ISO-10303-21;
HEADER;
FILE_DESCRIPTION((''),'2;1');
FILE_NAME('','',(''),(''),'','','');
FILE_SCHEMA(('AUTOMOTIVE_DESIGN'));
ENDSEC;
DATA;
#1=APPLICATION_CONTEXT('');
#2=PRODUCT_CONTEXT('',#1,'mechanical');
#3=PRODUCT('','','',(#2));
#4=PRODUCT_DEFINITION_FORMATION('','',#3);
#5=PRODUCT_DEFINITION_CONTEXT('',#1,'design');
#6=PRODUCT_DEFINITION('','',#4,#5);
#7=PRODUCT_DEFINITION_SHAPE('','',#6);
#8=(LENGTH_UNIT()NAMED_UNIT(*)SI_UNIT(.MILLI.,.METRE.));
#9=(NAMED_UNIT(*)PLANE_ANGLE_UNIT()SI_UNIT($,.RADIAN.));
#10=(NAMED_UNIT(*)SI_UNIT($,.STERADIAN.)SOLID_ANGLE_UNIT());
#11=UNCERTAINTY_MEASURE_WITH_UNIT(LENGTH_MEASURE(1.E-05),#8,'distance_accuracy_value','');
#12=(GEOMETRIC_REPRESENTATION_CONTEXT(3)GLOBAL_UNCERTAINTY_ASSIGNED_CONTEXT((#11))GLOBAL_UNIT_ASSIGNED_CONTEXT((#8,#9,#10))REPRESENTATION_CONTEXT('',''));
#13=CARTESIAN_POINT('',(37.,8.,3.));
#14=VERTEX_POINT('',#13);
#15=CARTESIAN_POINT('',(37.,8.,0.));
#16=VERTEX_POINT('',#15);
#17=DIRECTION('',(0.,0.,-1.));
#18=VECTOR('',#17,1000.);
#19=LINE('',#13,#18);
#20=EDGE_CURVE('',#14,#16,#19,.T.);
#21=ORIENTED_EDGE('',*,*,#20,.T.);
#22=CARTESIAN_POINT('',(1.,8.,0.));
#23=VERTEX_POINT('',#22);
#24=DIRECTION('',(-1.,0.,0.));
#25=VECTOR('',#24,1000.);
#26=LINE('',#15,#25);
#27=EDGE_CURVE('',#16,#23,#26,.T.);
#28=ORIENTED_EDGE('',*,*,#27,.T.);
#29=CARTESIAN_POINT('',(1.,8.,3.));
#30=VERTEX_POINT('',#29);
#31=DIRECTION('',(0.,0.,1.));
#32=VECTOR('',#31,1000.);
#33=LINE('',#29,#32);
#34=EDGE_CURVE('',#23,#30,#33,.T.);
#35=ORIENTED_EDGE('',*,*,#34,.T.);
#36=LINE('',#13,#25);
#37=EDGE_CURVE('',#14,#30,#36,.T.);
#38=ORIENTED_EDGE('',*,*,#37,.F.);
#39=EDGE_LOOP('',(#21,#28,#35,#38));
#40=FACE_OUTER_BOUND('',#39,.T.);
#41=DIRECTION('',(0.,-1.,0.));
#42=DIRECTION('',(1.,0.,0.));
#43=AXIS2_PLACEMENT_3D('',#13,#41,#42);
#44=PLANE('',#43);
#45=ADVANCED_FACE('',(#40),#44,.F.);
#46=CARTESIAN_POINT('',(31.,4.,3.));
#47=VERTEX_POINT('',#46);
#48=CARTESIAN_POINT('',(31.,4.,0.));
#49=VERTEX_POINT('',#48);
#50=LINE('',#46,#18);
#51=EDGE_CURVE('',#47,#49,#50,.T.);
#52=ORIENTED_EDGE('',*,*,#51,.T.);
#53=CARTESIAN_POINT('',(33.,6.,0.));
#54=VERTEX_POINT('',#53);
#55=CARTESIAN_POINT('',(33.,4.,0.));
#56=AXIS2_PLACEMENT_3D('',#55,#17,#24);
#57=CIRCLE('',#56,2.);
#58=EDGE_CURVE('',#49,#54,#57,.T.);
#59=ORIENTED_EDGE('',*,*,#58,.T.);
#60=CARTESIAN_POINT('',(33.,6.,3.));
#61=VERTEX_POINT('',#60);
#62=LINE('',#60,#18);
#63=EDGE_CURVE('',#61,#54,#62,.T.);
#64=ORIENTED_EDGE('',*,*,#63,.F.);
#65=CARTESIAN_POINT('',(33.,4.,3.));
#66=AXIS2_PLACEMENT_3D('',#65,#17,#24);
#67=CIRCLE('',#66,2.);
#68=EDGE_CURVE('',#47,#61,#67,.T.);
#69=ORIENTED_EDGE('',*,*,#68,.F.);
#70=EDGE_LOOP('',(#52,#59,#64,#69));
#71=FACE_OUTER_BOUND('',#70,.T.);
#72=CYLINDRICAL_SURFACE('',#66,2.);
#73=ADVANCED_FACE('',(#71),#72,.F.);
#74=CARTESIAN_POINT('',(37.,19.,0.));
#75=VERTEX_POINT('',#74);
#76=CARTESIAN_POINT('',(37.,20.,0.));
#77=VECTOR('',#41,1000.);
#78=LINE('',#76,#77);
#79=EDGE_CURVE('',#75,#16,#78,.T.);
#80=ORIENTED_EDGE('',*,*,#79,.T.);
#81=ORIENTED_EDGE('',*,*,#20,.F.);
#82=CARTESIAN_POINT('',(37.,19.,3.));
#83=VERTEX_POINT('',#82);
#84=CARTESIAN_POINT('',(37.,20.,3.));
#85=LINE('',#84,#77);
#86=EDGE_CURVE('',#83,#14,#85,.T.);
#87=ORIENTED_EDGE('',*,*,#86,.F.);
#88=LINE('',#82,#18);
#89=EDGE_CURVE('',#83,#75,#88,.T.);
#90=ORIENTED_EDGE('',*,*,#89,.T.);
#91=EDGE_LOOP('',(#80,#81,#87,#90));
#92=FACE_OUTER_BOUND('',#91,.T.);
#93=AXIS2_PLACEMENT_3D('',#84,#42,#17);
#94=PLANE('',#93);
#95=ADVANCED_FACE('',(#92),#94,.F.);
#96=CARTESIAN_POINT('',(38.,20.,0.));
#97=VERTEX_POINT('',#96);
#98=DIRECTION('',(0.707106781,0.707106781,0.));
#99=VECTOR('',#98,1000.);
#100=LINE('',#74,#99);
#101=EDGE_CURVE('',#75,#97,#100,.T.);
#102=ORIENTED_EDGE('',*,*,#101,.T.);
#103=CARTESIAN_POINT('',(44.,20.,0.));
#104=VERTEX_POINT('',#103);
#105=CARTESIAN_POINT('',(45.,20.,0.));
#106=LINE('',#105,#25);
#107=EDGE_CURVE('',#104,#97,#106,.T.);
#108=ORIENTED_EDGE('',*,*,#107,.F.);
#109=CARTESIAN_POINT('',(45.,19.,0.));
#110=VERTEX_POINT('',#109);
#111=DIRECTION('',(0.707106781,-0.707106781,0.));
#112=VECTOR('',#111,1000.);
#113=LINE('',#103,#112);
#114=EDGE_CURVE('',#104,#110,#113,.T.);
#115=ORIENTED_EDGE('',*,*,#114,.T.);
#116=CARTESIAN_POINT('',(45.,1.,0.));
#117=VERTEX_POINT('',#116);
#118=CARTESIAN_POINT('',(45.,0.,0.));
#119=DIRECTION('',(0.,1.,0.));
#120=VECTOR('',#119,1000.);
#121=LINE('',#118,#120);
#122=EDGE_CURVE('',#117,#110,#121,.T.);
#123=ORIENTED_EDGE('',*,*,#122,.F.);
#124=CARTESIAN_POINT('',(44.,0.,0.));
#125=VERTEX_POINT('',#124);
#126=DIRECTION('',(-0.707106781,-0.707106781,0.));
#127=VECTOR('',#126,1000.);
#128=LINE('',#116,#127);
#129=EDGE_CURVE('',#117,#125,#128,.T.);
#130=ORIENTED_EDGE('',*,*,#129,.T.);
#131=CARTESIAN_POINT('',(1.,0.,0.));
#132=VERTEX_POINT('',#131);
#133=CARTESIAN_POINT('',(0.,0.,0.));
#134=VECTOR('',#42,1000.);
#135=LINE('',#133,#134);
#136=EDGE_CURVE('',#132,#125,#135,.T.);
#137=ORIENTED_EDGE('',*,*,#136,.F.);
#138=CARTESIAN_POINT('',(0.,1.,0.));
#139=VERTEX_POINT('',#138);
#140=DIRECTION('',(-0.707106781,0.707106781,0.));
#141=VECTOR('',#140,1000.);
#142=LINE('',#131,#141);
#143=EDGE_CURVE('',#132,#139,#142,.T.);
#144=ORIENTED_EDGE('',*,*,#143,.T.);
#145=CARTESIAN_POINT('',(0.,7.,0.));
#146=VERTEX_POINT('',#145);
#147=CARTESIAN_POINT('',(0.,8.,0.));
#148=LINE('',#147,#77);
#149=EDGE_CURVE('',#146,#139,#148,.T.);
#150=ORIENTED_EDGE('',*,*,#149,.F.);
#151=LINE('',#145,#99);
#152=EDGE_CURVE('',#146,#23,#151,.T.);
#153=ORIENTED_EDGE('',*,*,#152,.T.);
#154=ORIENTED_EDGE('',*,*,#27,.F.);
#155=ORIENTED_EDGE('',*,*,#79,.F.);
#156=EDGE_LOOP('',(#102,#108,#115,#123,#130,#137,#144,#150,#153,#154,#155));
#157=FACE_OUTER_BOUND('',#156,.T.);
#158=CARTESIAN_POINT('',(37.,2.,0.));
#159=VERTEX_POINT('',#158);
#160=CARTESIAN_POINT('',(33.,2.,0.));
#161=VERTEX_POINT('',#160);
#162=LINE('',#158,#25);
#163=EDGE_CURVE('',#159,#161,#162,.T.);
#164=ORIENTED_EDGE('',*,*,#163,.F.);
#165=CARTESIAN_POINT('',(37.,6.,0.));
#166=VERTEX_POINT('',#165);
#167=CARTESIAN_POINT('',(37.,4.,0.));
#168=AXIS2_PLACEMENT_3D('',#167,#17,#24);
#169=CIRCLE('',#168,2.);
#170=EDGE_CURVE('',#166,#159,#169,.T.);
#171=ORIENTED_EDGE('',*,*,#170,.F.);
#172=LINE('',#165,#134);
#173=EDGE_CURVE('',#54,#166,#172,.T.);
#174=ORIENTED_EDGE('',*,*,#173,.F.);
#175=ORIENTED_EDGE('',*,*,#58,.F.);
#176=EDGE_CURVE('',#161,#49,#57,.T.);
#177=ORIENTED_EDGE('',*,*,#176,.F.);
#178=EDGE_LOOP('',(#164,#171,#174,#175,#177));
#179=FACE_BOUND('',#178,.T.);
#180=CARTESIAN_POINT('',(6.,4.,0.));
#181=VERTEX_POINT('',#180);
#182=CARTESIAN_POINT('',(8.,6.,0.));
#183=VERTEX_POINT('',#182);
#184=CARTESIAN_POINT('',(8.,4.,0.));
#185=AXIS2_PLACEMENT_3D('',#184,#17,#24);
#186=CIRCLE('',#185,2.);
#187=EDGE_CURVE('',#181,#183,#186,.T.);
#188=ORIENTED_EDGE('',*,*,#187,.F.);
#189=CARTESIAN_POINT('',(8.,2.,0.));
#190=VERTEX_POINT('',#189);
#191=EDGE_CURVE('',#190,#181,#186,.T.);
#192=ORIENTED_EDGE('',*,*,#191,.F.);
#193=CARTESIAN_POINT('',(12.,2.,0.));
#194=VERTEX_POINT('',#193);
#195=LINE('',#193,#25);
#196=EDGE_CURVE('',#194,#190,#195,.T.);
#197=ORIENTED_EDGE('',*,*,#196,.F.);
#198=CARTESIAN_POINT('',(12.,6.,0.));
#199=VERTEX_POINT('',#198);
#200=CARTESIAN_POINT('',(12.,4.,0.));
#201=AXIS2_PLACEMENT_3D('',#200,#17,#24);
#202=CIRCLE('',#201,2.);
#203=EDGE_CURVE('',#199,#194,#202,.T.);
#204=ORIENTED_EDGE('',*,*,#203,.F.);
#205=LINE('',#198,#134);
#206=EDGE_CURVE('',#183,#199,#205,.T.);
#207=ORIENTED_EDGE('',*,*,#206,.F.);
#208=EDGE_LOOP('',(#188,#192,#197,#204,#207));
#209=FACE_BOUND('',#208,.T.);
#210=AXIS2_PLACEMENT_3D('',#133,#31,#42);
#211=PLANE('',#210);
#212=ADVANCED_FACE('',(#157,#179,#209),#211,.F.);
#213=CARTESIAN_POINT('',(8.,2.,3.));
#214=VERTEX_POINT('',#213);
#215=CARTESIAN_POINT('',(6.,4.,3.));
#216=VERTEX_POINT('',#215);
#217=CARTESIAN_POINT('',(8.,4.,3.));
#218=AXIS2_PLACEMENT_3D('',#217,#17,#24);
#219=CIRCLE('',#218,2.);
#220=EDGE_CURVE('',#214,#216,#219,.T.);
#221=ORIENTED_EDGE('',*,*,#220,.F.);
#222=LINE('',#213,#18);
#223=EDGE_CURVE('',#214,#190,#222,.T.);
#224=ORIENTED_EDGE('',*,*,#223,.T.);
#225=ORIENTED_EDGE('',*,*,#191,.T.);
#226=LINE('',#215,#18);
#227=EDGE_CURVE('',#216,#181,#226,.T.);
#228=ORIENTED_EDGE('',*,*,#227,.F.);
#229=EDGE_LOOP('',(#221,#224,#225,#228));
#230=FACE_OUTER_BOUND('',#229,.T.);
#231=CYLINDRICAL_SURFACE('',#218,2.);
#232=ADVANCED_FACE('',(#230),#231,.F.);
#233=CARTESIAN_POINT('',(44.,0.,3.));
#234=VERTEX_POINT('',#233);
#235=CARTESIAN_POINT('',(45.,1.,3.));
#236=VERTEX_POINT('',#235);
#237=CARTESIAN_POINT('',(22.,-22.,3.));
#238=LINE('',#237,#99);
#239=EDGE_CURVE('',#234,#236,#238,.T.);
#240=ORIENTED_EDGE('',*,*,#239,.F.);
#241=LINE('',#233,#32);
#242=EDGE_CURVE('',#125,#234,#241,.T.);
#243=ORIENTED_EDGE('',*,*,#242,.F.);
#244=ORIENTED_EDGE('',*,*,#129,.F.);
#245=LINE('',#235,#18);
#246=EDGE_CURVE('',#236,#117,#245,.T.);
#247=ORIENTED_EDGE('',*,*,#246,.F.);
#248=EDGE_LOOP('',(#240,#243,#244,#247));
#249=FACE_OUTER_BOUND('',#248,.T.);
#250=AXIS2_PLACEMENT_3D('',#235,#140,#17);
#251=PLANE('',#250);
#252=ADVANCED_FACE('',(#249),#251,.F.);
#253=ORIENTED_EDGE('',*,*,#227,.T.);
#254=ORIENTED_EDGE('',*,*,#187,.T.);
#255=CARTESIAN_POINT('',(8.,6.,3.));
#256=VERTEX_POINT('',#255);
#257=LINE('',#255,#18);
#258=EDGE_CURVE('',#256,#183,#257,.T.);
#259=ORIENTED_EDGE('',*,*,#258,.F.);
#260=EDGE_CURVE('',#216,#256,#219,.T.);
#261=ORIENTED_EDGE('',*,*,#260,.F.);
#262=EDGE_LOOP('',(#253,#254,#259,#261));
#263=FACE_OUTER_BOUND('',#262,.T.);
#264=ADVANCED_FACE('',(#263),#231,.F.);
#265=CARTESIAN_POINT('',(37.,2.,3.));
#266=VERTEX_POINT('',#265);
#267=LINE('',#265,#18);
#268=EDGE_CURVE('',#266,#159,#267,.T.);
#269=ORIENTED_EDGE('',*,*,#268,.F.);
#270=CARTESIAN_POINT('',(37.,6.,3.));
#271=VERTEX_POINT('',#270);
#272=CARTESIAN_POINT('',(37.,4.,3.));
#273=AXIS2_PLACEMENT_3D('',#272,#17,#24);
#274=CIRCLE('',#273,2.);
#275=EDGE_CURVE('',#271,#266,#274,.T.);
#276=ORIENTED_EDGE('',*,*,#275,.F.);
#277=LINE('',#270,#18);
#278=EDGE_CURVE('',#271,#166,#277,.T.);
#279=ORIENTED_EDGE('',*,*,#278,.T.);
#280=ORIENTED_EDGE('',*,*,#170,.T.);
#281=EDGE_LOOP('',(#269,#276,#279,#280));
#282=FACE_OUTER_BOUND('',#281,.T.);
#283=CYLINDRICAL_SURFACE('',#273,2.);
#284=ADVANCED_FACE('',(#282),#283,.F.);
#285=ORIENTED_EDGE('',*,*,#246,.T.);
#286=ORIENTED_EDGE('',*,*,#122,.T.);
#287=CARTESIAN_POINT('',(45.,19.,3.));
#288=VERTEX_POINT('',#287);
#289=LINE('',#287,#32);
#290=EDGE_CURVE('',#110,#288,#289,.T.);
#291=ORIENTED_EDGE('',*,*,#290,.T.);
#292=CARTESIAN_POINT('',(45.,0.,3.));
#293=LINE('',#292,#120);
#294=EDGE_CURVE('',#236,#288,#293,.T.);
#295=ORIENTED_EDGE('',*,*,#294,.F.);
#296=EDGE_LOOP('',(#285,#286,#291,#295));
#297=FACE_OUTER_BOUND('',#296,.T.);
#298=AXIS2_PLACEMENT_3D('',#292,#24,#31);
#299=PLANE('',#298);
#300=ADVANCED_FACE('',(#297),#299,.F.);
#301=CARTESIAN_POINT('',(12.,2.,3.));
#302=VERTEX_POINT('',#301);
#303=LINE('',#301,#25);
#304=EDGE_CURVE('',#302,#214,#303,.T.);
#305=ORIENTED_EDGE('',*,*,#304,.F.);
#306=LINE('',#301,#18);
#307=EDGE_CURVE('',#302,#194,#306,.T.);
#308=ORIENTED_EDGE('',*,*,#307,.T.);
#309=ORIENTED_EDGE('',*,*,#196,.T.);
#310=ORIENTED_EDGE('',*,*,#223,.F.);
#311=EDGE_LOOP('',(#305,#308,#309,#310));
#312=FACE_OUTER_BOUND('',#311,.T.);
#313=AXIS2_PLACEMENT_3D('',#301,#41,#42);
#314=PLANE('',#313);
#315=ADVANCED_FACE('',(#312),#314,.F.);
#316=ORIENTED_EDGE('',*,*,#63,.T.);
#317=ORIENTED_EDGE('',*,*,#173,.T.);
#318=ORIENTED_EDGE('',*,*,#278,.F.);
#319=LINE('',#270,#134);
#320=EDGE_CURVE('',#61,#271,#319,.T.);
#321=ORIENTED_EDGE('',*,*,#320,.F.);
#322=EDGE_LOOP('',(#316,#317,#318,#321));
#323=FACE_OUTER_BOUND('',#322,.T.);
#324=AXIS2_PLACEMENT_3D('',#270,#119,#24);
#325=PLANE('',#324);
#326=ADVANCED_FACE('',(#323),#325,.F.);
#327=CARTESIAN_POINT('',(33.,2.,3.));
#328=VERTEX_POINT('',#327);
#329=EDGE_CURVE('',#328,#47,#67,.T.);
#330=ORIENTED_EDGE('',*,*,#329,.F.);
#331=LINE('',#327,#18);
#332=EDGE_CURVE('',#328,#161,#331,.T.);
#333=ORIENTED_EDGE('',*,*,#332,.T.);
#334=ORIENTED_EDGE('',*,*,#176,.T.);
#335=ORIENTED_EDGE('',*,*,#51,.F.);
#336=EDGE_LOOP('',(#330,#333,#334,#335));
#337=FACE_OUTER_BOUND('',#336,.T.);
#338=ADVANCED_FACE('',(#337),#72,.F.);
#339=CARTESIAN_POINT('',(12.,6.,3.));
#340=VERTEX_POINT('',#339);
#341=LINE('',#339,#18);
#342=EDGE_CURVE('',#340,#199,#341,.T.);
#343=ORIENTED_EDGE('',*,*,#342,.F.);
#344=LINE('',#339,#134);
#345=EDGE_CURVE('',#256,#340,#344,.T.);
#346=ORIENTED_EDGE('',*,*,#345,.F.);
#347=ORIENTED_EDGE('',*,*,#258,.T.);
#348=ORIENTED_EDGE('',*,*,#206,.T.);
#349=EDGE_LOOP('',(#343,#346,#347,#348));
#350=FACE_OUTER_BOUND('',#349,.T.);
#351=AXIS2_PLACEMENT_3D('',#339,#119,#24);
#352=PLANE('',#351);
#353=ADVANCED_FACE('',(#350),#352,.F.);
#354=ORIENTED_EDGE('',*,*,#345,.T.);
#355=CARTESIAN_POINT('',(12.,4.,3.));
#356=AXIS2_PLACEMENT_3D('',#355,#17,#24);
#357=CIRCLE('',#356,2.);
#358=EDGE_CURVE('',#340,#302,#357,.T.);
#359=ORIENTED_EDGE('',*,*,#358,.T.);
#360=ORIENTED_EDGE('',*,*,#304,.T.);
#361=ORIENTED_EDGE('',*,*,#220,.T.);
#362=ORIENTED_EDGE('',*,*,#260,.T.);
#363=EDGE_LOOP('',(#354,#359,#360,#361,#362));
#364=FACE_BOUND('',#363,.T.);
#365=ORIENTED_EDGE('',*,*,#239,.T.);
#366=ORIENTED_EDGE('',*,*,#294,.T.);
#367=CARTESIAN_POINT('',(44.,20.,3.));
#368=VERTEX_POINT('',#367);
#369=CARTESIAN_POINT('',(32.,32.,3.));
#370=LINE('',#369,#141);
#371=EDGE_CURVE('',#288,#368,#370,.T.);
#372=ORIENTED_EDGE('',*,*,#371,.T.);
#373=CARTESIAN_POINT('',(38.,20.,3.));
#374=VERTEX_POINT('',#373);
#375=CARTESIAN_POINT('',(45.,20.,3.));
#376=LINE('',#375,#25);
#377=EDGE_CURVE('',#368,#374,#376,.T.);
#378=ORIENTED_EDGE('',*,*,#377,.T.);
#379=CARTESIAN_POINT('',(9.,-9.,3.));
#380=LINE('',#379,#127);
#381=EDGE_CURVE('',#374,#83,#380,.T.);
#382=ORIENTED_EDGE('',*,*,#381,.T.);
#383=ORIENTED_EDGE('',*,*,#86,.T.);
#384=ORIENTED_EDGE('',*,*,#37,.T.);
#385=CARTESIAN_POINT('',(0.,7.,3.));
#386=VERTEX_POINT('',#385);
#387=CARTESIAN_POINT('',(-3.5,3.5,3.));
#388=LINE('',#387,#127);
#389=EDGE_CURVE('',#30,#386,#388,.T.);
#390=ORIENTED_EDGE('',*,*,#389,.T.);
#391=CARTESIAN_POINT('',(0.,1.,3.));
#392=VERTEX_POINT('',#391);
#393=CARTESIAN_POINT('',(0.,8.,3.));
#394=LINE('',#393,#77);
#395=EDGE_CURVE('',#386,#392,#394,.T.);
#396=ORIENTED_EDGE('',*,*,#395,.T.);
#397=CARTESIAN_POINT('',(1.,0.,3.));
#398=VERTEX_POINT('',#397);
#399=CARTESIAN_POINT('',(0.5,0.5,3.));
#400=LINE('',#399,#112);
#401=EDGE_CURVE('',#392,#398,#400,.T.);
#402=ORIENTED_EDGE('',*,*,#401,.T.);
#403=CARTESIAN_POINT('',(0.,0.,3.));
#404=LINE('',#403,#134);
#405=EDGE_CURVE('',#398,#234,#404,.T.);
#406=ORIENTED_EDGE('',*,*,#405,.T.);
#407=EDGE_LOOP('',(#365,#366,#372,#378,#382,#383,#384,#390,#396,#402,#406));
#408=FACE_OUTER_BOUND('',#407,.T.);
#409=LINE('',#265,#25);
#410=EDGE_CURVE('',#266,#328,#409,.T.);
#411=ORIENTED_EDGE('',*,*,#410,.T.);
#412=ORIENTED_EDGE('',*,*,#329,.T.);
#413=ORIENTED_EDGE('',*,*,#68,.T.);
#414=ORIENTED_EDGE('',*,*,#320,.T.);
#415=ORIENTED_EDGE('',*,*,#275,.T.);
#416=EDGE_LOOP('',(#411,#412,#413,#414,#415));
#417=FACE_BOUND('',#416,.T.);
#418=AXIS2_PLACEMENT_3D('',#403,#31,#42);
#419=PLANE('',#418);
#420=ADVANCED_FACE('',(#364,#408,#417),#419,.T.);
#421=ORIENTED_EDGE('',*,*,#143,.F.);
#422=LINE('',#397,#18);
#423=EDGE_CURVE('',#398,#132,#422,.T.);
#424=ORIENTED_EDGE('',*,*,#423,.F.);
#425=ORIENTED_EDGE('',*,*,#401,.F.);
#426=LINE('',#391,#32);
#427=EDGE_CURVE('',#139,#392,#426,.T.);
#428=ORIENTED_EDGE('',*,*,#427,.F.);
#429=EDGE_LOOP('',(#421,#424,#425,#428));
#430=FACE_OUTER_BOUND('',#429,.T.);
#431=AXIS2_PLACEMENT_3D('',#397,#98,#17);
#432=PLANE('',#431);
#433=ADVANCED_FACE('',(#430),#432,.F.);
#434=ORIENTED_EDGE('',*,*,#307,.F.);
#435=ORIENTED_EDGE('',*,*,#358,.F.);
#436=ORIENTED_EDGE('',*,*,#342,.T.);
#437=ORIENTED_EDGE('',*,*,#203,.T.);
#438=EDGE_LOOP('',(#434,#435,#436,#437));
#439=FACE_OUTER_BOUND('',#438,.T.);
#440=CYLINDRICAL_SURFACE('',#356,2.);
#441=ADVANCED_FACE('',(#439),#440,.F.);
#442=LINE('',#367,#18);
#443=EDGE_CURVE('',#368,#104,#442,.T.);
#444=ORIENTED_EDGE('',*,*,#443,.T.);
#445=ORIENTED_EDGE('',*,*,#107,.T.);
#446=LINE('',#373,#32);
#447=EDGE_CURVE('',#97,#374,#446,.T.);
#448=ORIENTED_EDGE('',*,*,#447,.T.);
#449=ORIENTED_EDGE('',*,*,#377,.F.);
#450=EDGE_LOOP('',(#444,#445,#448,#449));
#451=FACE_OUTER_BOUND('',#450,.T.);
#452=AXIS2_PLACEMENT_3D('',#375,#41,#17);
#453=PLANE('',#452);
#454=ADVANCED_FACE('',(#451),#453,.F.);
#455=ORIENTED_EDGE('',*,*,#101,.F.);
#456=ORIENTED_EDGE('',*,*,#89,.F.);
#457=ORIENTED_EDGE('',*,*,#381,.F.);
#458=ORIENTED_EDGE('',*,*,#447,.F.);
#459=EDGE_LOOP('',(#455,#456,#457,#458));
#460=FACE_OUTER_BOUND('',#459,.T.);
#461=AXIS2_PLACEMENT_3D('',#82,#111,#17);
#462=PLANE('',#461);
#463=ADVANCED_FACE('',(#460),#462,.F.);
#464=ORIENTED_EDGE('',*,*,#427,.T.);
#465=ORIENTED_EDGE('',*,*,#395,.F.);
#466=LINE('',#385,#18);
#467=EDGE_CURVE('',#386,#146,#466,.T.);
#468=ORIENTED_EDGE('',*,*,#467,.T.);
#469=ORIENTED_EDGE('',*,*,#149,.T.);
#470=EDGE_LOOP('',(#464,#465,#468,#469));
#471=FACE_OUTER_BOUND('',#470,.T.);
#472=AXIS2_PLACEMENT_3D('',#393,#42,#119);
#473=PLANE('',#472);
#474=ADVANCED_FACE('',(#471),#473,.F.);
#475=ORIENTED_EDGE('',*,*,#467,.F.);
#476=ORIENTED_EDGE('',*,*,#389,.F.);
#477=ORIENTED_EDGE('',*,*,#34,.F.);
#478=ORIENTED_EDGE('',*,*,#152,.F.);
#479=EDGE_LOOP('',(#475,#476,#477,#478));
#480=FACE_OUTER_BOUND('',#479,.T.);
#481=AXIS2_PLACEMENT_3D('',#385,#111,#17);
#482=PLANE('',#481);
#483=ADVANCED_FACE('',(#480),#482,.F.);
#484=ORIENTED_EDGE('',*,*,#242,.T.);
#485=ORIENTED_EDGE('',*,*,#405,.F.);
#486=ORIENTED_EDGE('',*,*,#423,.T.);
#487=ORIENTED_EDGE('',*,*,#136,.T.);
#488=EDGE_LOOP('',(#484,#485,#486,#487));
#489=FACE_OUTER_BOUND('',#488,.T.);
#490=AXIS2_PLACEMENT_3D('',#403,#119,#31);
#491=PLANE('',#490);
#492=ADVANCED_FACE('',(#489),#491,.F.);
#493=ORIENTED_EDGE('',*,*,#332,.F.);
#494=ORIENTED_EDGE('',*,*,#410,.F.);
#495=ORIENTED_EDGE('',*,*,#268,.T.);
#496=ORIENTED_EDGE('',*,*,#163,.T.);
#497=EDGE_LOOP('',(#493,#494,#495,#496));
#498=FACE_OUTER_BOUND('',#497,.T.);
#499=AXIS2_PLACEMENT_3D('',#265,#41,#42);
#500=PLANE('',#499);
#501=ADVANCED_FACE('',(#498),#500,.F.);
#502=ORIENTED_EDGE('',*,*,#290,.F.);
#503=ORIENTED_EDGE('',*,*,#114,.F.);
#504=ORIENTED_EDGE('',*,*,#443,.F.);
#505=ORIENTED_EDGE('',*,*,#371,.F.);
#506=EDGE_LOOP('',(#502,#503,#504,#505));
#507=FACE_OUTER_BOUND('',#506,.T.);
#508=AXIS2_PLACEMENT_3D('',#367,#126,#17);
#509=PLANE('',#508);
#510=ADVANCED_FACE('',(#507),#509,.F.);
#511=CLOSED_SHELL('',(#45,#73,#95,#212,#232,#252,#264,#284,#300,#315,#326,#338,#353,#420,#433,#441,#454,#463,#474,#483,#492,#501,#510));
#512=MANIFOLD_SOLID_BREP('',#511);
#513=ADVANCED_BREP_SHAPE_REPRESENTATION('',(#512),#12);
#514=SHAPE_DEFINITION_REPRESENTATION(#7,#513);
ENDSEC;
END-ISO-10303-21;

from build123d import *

# Parameters (mm, degrees)
BOSS_EXTRUDE1_DEPTH = 3
CUT_EXTRUDE1_DEPTH  = 3
CHAMFER1_SIZE       = 1


with BuildPart() as part:
    # Sketch1 → Boss-Extrude1 (new body)
    with BuildSketch(Plane.XY):
        Polygon((0, 0), (45, 0), (45, 20), (37, 20), (37, 8), (0, 8), align=None)
    extrude(amount=BOSS_EXTRUDE1_DEPTH)

    # Sketch2 → Cut-Extrude1 (cut)
    with BuildSketch(Plane(origin=(0, 0, 0), x_dir=(-1, 0, 0), z_dir=(0, 0, -1))):
        with BuildLine():
            Line((-37, 6), (-33, 6))
            ThreePointArc((-33, 6), (-31, 4), (-33, 2))
            Line((-33, 2), (-37, 2))
            ThreePointArc((-37, 2), (-39, 4), (-37, 6))
        make_face()
        with BuildLine():
            Line((-12, 6), (-8, 6))
            ThreePointArc((-8, 6), (-6, 4), (-8, 2))
            Line((-8, 2), (-12, 2))
            ThreePointArc((-12, 2), (-14, 4), (-12, 6))
        make_face()
    extrude(amount=-CUT_EXTRUDE1_DEPTH, mode=Mode.SUBTRACT)

    # Chamfer1
    chamfer1_edges = [part.edges().sort_by_distance(p)[0] for p in [
        (0, 8, 1.5),
        (37, 20, 1.5),
        (45, 20, 1.5),
        (45, 0, 1.5),
        (0, 0, 1.5),
    ]]
    chamfer(chamfer1_edges, length=CHAMFER1_SIZE)


solid = part.part
